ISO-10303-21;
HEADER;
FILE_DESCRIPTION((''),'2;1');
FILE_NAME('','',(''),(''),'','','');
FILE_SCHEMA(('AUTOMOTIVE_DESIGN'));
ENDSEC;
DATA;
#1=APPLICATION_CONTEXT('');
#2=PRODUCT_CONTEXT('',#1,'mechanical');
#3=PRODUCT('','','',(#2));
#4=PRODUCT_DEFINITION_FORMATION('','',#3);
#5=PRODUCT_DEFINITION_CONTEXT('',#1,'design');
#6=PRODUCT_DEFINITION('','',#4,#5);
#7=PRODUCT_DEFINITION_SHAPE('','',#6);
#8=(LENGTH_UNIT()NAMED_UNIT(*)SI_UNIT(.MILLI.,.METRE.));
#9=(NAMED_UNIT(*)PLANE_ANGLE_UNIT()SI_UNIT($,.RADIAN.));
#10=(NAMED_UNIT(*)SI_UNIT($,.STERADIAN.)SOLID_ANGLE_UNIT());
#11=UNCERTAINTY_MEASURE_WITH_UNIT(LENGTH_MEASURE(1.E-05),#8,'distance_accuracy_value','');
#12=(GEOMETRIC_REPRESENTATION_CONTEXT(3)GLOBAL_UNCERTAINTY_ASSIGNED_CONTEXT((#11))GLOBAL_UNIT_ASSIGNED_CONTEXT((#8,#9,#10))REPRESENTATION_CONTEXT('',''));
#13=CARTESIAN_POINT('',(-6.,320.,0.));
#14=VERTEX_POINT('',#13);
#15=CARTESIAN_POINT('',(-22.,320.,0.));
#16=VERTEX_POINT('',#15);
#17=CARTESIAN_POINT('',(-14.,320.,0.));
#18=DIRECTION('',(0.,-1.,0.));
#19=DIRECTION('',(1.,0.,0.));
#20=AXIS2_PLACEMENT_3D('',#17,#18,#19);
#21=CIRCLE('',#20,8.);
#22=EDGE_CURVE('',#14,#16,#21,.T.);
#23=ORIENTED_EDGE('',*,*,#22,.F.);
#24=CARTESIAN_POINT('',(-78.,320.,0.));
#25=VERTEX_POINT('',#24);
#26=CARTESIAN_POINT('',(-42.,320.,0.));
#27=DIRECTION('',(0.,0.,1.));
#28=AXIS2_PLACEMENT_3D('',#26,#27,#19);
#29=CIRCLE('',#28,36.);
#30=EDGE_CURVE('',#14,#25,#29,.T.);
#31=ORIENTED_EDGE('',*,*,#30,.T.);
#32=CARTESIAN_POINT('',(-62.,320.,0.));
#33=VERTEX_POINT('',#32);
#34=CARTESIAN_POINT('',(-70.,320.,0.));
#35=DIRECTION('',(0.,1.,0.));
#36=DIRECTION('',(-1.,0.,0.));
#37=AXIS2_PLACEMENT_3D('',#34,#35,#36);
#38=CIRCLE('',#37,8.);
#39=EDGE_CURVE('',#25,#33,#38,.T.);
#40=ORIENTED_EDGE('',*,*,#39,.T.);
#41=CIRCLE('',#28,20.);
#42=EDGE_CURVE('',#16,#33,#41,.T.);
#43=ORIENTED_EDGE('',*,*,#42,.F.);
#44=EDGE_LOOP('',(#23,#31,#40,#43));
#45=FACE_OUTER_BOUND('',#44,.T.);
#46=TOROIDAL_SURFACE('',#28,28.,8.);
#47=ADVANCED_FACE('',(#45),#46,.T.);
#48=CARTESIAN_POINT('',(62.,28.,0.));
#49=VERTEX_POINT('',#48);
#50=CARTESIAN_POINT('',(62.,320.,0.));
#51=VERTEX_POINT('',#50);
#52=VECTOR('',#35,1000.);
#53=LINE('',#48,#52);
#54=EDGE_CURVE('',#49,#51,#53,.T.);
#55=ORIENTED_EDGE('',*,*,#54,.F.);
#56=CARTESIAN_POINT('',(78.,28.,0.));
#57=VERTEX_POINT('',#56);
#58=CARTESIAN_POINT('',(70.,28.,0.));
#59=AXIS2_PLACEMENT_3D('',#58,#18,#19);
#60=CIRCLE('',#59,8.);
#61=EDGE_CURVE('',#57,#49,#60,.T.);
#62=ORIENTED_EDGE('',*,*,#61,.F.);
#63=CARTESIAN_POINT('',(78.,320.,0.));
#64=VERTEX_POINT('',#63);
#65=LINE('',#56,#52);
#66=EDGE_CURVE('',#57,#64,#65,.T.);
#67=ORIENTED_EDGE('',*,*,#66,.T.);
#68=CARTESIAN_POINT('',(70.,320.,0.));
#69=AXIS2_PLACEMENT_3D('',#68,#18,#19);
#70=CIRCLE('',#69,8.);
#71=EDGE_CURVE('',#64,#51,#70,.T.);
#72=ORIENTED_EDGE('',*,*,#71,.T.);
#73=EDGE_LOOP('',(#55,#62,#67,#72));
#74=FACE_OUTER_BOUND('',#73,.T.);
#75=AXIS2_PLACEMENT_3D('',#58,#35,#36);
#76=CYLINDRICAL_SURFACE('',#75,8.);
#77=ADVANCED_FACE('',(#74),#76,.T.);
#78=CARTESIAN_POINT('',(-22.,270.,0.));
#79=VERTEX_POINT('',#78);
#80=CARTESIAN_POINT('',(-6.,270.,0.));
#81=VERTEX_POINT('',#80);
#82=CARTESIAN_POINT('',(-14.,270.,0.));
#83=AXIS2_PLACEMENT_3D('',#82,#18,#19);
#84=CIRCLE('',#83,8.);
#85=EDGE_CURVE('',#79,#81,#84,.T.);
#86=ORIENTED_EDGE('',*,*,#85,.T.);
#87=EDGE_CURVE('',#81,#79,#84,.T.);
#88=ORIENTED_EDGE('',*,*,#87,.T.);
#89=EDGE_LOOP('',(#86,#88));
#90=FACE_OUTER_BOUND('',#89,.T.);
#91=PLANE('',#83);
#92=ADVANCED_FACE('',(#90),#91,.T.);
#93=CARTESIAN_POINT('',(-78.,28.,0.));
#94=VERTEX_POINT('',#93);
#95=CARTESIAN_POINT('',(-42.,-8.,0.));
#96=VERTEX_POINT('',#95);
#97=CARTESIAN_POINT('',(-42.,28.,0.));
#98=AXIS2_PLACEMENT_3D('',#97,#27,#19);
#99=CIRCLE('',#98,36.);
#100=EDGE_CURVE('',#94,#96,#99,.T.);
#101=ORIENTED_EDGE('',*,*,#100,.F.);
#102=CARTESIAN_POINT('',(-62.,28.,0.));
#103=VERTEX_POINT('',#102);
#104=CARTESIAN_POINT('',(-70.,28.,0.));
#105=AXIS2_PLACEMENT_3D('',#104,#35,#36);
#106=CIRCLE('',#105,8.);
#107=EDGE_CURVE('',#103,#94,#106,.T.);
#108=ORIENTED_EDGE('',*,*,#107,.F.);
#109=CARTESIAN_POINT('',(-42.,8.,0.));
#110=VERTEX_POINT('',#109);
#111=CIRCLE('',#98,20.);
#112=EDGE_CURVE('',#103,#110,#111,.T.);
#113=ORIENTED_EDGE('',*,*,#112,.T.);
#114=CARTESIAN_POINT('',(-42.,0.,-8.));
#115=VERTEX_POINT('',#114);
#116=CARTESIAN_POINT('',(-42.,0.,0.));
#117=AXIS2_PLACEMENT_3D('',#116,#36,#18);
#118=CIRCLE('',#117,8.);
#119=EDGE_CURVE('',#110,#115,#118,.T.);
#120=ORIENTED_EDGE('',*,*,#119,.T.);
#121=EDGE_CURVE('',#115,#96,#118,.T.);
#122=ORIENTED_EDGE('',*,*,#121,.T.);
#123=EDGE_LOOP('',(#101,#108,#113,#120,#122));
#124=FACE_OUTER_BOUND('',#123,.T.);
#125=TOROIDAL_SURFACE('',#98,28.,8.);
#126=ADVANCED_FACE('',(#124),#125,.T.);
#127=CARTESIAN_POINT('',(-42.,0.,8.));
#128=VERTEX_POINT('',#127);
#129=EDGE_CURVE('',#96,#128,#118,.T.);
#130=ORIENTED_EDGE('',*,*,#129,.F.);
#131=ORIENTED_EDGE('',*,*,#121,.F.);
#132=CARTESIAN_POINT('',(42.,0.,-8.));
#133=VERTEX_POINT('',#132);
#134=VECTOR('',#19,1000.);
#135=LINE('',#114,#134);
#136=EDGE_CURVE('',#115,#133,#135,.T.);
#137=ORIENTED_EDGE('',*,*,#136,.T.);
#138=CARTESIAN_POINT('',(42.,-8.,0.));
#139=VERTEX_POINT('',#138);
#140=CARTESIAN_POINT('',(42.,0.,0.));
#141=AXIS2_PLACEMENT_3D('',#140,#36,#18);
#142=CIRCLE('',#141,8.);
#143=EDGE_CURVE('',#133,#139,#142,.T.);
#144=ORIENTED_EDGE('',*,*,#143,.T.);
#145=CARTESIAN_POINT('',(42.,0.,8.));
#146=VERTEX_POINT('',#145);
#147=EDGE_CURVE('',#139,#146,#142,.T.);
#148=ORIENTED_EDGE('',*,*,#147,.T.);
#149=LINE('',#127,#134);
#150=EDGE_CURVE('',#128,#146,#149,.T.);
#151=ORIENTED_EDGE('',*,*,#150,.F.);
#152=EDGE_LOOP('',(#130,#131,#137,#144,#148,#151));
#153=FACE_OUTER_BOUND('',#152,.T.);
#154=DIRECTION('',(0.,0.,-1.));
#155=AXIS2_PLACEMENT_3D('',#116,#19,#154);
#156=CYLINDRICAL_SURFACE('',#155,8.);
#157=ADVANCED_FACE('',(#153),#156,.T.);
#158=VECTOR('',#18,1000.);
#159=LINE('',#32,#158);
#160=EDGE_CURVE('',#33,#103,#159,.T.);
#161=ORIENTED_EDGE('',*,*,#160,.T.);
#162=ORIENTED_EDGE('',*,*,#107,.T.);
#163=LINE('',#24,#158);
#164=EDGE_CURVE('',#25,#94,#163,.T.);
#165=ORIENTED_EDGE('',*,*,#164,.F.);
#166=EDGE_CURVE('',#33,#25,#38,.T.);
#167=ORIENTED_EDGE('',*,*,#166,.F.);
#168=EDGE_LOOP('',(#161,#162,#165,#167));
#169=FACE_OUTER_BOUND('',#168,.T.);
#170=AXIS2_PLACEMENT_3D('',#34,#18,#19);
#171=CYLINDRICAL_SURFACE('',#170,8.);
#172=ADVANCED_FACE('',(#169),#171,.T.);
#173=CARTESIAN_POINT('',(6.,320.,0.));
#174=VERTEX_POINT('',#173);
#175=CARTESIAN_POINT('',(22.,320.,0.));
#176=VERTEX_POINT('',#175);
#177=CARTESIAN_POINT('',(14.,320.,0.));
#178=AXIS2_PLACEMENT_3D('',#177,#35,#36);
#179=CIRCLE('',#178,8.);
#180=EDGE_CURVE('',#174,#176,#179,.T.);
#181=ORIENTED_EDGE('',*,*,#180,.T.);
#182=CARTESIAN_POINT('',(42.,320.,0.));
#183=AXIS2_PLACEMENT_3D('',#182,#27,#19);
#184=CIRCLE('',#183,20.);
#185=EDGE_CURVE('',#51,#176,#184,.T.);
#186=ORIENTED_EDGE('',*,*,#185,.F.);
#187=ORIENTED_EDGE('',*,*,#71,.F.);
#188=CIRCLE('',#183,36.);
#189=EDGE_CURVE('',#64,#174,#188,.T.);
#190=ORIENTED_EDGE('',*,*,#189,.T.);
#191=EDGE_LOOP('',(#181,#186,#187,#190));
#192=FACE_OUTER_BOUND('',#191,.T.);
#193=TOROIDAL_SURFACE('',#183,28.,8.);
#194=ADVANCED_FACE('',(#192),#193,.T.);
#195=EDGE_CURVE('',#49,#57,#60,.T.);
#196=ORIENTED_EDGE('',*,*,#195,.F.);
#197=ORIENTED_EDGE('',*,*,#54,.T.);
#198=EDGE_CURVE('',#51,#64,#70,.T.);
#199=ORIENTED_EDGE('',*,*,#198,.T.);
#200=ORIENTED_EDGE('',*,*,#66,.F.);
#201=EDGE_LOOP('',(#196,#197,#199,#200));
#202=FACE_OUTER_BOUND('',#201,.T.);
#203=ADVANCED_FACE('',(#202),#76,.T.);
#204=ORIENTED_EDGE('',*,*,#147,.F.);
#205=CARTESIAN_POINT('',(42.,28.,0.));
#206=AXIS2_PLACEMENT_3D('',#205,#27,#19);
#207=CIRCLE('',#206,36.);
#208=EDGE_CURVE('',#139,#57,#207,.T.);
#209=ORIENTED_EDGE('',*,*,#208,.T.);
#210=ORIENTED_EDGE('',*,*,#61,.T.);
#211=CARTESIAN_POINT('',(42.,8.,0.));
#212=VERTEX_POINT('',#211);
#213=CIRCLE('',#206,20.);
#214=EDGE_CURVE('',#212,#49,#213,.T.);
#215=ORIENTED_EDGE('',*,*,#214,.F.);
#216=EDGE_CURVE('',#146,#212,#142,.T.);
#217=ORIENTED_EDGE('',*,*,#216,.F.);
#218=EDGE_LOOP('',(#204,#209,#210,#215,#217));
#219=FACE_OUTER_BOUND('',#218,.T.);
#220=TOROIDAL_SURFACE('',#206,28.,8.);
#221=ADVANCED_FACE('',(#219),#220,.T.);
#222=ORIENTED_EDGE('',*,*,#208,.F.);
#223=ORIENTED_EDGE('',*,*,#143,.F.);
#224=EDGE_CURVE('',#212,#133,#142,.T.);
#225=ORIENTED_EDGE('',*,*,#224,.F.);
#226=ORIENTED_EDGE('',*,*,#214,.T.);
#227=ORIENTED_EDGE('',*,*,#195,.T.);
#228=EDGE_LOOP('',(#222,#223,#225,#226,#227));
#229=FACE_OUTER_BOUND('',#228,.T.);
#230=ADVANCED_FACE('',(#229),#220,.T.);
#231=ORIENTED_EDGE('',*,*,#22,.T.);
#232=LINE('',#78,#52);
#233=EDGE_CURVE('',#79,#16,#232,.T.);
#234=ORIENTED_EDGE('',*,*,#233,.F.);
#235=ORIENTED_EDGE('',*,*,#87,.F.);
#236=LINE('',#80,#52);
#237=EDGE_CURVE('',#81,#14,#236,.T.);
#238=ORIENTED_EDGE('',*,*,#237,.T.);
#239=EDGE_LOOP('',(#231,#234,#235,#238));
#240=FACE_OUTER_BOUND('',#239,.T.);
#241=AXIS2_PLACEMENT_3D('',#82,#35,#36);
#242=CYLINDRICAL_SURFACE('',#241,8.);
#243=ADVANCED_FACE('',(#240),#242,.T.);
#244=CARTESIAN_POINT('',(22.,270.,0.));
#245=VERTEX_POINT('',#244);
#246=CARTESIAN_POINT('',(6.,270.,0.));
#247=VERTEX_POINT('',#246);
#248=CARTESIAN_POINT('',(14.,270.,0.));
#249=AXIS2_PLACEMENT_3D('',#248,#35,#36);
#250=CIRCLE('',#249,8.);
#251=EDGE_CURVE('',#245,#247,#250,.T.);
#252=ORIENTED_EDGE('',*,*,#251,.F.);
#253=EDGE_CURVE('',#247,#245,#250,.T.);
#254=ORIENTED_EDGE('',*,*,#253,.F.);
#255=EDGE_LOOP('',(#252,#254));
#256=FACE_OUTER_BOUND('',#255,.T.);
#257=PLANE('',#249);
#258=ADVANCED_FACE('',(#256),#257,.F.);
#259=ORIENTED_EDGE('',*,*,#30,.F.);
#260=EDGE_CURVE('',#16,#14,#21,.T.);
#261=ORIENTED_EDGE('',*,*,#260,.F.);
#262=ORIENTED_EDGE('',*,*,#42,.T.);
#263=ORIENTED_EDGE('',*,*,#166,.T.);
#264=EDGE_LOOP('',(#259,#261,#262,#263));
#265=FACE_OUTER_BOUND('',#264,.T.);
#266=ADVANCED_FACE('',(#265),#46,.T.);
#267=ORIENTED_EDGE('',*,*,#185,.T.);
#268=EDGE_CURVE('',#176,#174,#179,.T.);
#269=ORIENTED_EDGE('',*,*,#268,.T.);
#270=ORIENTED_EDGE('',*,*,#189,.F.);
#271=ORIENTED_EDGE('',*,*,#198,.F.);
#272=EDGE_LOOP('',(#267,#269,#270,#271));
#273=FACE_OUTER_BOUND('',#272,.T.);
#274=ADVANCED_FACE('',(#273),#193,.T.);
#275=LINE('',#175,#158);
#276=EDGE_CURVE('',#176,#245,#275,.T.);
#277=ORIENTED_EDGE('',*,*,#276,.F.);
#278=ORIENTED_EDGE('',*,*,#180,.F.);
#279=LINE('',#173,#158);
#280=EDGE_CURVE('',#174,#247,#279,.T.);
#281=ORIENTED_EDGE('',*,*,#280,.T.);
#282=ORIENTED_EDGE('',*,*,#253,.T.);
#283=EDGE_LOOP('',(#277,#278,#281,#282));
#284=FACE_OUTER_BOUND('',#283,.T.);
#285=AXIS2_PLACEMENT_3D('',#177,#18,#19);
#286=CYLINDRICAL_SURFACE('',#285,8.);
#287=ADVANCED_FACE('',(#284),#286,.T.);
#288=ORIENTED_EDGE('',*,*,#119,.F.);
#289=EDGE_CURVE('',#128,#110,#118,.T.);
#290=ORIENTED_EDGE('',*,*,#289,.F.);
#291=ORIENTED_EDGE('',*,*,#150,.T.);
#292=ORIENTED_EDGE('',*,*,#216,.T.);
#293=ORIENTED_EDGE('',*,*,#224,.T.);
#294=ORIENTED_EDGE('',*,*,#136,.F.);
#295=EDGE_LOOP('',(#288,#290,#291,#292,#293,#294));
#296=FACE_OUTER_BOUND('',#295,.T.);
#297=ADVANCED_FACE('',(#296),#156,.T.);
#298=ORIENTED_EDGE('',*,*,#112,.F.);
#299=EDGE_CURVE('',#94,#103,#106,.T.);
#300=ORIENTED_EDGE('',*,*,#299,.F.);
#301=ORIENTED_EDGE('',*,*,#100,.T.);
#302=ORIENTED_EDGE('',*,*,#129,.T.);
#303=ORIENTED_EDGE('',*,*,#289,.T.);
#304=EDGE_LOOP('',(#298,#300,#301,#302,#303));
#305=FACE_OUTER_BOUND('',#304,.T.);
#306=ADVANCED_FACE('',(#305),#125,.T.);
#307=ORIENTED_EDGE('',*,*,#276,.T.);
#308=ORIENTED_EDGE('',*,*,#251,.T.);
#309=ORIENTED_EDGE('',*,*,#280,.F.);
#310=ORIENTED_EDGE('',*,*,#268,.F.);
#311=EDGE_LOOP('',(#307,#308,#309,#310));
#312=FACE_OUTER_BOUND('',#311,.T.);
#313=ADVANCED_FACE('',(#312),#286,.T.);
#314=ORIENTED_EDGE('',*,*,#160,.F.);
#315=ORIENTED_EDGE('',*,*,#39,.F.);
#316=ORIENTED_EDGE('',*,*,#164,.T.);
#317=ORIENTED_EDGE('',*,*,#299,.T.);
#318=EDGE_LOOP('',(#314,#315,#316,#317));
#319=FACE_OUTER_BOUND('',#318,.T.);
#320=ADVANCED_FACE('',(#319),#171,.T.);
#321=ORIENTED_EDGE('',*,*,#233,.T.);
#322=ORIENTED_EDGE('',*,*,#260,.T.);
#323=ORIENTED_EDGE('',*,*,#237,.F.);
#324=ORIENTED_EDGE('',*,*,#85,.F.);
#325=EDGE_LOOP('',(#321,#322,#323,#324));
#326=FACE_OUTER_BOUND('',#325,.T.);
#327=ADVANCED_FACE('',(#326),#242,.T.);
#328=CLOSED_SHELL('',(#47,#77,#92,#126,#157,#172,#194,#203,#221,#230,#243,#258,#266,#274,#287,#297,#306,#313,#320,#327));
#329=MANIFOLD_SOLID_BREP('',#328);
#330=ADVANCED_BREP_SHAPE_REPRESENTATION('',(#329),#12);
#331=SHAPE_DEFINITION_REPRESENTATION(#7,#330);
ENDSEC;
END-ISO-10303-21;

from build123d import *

# Parameters (mm, degrees)
SWEEP_1_PROFILE_R = 8


with BuildPart() as part:
    # 扫描1: sweep along a path in 草图1
    with BuildLine(Plane.XY) as sweep_1_path:
        Line((-14, 270), (-14, 320))
        ThreePointArc((-14, 320), (-42, 348), (-70, 320))
        Line((-70, 320), (-70, 28))
        ThreePointArc((-70, 28), (-61.798989873, 8.201010127), (-42, 0))
        Line((-42, 0), (42, 0))
        ThreePointArc((42, 0), (61.798989873, 8.201010127), (70, 28))
        Line((70, 28), (70, 320))
        ThreePointArc((70, 320), (42, 348), (14, 320))
        Line((14, 320), (14, 270))
    # 扫描1 profile (on start of the path) → 扫描1 (sweep)
    with BuildSketch(Plane(origin=(-14, 270, 0), x_dir=(1, 0, 0), z_dir=(0, 1, 0))):
        Circle(SWEEP_1_PROFILE_R)
    sweep(path=sweep_1_path.line)


solid = part.part
